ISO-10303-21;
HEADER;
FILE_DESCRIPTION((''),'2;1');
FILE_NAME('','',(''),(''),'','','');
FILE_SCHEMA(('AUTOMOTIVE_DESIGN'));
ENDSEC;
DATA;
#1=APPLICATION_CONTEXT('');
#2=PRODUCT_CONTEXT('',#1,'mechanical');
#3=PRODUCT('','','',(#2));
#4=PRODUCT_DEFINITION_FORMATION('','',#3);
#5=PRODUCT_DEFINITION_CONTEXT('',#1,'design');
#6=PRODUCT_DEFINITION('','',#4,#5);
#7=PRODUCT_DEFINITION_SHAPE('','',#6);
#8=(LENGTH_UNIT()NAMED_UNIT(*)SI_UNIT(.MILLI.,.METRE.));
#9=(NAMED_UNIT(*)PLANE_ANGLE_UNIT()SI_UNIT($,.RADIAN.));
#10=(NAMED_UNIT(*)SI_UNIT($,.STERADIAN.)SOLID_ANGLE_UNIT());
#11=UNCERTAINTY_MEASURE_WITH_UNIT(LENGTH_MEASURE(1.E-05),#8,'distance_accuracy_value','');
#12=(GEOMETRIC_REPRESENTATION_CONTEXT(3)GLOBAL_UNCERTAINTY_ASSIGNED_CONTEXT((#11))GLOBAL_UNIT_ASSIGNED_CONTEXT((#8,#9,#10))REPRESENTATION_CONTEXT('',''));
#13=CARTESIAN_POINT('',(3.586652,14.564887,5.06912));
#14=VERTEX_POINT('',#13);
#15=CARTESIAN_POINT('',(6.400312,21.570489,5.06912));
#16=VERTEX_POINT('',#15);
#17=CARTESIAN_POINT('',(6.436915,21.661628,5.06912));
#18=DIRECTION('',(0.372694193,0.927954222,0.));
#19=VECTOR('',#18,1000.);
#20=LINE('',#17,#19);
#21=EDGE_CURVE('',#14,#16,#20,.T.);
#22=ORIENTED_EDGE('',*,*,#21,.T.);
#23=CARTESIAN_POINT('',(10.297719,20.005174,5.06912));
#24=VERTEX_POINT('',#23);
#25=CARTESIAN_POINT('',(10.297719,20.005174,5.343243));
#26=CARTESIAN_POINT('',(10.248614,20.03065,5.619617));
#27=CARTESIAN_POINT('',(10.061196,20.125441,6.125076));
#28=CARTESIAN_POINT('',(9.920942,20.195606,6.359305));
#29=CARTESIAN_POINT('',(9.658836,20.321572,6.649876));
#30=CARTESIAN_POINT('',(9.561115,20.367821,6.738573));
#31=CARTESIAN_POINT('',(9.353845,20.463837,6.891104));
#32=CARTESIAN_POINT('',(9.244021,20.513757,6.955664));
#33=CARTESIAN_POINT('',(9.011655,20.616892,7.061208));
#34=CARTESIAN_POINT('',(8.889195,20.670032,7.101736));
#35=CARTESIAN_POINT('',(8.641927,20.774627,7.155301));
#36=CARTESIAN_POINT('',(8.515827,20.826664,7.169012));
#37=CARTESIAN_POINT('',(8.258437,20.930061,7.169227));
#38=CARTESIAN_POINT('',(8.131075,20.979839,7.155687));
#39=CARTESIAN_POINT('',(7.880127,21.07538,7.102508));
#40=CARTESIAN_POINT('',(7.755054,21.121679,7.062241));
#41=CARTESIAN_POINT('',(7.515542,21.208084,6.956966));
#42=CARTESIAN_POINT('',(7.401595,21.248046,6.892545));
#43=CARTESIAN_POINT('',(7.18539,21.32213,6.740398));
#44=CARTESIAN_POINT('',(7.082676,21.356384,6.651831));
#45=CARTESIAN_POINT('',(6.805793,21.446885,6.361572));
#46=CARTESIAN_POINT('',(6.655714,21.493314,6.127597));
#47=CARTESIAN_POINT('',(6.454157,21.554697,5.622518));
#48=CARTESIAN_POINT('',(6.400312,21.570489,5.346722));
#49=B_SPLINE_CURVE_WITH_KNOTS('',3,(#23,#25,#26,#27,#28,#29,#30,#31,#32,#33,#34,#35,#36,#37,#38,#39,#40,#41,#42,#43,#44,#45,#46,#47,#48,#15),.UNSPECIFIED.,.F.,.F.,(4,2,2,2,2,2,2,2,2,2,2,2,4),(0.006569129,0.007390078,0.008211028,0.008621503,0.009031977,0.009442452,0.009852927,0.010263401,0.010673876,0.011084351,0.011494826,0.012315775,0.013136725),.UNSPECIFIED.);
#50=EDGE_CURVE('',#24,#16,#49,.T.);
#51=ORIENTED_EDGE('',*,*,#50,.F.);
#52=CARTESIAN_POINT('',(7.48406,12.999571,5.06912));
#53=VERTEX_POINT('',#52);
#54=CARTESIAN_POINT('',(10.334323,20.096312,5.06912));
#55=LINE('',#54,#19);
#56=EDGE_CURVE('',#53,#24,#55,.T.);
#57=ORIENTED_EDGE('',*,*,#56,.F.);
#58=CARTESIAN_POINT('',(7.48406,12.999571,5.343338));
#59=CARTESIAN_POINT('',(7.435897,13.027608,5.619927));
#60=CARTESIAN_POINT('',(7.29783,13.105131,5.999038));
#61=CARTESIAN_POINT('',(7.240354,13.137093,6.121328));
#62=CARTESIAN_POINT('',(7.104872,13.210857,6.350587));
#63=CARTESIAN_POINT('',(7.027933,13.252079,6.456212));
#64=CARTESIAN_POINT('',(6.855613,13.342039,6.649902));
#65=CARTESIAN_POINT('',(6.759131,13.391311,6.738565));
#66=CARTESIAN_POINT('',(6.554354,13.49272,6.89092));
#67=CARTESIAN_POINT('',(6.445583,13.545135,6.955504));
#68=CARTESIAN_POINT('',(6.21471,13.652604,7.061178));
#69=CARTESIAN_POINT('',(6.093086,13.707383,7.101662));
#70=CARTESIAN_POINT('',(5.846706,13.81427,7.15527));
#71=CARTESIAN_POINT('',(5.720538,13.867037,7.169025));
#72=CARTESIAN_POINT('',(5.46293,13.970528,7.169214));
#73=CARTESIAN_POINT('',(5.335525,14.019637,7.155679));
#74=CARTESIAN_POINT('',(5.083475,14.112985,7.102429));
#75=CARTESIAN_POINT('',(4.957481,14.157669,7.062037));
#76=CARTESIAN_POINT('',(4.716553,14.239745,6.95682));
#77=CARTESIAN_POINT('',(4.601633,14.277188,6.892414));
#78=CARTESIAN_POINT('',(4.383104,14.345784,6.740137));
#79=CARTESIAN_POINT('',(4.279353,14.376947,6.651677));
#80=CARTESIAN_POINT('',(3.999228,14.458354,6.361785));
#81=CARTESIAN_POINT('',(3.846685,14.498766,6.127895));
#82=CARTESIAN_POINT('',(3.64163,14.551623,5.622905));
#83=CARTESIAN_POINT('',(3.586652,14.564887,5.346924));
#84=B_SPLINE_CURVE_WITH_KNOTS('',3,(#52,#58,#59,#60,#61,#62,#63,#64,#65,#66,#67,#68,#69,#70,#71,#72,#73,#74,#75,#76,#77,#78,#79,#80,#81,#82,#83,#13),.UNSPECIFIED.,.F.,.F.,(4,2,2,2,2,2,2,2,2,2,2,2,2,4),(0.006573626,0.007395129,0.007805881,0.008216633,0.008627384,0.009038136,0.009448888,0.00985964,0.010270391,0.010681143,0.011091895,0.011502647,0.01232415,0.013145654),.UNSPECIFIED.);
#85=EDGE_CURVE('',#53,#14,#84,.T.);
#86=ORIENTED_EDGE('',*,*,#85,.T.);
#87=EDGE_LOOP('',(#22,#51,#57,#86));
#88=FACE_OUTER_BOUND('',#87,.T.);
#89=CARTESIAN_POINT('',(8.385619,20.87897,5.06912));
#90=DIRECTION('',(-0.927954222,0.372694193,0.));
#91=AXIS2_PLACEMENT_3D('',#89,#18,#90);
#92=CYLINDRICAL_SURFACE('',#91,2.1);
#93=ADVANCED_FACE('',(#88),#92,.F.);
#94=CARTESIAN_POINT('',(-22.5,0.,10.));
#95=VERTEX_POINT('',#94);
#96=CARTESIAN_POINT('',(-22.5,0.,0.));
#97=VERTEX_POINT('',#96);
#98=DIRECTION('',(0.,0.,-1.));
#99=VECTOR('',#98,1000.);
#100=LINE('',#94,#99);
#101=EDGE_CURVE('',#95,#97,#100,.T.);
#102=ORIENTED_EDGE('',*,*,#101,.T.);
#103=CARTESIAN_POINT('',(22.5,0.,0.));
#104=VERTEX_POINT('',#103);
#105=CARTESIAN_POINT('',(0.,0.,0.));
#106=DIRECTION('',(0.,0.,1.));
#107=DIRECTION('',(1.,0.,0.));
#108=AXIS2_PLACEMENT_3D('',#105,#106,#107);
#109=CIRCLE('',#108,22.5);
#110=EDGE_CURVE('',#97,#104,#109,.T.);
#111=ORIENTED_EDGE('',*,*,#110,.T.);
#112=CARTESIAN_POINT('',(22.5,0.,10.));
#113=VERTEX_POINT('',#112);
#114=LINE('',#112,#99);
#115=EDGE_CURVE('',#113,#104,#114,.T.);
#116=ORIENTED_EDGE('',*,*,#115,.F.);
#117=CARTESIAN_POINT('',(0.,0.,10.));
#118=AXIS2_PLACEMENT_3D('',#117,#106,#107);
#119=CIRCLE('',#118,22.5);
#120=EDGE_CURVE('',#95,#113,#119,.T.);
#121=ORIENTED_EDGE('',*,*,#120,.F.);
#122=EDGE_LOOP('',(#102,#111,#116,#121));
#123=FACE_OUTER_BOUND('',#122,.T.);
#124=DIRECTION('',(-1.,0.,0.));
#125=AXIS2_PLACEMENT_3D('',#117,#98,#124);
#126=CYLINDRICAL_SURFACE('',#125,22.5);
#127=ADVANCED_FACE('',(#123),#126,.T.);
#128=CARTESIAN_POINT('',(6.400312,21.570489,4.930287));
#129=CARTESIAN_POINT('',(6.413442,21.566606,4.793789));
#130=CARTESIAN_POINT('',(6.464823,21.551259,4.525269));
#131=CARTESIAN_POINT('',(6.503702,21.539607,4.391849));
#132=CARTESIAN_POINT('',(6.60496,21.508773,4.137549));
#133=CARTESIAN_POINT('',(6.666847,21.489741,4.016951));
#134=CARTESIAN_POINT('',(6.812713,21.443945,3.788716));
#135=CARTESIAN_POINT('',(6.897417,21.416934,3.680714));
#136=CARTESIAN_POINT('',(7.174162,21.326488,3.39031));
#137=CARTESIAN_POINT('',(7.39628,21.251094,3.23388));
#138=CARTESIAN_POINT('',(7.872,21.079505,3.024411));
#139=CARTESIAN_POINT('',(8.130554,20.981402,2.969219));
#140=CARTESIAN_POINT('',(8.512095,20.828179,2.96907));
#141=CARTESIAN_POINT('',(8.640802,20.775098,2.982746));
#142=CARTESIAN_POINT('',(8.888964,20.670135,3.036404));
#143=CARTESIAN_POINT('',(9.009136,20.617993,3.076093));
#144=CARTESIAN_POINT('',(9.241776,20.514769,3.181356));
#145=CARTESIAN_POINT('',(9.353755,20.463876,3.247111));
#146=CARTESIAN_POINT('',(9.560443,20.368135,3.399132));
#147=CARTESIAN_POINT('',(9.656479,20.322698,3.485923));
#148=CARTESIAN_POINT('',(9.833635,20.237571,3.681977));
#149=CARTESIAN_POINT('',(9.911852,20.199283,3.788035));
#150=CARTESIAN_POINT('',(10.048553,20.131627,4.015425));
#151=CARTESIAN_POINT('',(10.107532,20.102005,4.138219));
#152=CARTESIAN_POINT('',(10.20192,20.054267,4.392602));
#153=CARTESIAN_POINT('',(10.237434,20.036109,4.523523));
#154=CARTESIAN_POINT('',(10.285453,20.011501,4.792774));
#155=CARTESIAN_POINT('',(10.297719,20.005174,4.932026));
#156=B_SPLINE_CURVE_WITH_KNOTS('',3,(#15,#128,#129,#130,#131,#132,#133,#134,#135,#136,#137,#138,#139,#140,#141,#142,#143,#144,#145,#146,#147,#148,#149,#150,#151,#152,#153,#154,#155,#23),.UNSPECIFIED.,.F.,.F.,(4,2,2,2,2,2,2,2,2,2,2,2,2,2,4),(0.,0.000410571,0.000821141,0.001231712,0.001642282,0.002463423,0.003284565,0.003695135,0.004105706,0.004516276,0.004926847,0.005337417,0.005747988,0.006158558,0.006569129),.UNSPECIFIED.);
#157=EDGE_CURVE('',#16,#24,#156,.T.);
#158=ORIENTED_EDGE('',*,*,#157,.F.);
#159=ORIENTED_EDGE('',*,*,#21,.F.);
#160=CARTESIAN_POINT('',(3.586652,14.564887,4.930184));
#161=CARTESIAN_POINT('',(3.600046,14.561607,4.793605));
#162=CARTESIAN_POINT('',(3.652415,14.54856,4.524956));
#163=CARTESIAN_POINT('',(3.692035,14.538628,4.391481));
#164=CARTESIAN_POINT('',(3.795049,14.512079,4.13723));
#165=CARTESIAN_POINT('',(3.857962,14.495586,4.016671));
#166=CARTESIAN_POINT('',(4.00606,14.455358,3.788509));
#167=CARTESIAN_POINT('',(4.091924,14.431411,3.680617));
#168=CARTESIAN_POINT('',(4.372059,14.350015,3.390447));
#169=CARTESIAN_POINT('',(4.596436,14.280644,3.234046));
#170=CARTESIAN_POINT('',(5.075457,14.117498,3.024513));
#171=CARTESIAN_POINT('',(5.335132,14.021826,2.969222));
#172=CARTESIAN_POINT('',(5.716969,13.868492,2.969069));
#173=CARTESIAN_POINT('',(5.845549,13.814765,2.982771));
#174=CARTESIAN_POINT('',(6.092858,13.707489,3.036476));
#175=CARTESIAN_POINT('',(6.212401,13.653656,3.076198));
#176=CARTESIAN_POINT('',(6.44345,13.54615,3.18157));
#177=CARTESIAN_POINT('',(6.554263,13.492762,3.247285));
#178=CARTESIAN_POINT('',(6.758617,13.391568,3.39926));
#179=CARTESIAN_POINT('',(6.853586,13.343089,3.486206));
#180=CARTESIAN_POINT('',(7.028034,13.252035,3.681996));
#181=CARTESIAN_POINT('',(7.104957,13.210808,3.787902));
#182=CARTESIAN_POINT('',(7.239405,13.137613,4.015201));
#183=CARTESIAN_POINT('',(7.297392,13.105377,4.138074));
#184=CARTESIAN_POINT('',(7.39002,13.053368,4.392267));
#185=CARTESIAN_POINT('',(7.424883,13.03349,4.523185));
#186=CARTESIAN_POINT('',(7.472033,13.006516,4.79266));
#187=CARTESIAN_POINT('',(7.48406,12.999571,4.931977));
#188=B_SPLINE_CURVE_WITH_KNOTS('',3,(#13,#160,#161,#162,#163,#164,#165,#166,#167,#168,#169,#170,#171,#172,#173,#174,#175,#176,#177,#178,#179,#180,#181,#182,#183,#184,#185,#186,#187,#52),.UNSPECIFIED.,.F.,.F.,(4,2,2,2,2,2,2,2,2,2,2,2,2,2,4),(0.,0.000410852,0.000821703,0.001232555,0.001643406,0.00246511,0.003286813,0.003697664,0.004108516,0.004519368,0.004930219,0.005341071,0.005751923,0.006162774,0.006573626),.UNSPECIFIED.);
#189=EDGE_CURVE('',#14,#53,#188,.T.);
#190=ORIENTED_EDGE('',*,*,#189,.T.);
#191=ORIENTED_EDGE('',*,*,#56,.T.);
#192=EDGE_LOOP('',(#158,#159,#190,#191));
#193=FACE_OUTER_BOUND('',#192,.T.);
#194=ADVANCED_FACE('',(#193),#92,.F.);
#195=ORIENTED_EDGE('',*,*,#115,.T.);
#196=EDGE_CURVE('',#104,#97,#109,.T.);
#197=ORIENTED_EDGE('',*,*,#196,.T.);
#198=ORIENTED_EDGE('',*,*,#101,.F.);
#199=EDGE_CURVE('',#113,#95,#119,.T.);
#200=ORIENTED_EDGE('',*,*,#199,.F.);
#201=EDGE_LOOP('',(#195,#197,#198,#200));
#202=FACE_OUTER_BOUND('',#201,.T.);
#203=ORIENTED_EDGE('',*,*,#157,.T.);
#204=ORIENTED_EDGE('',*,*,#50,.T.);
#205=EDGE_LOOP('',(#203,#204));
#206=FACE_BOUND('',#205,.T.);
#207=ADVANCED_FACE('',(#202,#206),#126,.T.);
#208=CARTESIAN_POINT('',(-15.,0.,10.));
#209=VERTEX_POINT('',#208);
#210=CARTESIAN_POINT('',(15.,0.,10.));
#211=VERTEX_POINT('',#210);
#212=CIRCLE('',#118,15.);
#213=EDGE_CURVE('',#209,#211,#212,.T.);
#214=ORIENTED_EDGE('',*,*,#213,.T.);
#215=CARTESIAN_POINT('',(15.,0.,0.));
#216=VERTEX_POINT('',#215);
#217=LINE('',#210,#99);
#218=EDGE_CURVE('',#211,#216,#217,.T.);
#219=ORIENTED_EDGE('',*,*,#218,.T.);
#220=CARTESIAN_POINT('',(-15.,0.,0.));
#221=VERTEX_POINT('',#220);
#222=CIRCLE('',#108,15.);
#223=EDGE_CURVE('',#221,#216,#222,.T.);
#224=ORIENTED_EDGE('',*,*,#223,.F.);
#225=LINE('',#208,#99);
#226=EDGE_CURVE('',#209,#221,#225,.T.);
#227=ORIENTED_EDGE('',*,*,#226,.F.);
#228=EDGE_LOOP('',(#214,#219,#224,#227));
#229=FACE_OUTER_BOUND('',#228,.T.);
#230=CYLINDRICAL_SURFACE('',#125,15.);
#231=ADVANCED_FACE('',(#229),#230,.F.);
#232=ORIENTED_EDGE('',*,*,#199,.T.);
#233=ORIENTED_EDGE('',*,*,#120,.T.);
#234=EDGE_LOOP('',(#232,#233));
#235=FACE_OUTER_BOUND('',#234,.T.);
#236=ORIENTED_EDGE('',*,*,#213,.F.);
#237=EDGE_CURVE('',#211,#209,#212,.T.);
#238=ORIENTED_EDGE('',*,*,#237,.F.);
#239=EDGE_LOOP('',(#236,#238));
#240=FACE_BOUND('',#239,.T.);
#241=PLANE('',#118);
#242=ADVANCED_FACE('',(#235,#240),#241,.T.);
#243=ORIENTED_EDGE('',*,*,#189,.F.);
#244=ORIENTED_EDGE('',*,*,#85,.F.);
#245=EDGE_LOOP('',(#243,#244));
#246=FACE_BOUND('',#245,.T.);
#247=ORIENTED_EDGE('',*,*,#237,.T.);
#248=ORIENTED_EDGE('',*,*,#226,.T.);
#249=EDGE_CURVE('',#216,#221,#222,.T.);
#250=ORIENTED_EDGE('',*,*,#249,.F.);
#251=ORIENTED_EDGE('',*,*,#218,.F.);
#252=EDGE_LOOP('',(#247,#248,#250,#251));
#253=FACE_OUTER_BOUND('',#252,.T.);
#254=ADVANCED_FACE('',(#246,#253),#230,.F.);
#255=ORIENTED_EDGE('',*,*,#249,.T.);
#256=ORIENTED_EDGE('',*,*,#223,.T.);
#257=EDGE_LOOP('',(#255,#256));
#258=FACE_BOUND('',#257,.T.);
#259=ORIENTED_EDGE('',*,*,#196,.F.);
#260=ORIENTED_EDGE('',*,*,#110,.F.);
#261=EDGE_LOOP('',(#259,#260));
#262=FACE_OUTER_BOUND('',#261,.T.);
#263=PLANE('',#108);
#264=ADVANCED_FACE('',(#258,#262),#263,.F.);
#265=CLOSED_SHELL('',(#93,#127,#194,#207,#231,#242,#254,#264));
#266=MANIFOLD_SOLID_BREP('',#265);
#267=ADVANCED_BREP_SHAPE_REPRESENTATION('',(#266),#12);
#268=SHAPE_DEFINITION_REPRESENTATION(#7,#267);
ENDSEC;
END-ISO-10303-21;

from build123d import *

# Parameters (mm, degrees)
SKETCH1_R              = 22.5
SKETCH1_R_2            = 15
BOSS_EXTRUDE1_DEPTH    = 10
M5_TAPPED_HOLE1_REACH  = 55.492
M5_TAPPED_HOLE1_BORE_R = 2.1


with BuildPart() as part:
    # Sketch1 → Boss-Extrude1 (new body)
    with BuildSketch(Plane.XY):
        Circle(SKETCH1_R)
        Circle(SKETCH1_R_2, mode=Mode.SUBTRACT)
    extrude(amount=BOSS_EXTRUDE1_DEPTH)

    # M5 Tapped Hole1 bore (on position points) → M5 Tapped Hole1 (cut, up to next)
    with BuildSketch(Plane(origin=(8.385619335, 20.878970002, 5.06911991), x_dir=(0.927954222329, -0.372694192686, 0), z_dir=(0.372694192686, 0.927954222329, 0)), mode=Mode.PRIVATE) as m5_tapped_hole1_sk1:
        Circle(M5_TAPPED_HOLE1_BORE_R)
    m5_tapped_hole1_tool1 = extrude(m5_tapped_hole1_sk1.sketch, amount=-M5_TAPPED_HOLE1_REACH, mode=Mode.PRIVATE) & part.part
    add(m5_tapped_hole1_tool1.solids().sort_by_distance((8.385619, 20.87897, 5.06912))[0], mode=Mode.SUBTRACT)


solid = part.part
